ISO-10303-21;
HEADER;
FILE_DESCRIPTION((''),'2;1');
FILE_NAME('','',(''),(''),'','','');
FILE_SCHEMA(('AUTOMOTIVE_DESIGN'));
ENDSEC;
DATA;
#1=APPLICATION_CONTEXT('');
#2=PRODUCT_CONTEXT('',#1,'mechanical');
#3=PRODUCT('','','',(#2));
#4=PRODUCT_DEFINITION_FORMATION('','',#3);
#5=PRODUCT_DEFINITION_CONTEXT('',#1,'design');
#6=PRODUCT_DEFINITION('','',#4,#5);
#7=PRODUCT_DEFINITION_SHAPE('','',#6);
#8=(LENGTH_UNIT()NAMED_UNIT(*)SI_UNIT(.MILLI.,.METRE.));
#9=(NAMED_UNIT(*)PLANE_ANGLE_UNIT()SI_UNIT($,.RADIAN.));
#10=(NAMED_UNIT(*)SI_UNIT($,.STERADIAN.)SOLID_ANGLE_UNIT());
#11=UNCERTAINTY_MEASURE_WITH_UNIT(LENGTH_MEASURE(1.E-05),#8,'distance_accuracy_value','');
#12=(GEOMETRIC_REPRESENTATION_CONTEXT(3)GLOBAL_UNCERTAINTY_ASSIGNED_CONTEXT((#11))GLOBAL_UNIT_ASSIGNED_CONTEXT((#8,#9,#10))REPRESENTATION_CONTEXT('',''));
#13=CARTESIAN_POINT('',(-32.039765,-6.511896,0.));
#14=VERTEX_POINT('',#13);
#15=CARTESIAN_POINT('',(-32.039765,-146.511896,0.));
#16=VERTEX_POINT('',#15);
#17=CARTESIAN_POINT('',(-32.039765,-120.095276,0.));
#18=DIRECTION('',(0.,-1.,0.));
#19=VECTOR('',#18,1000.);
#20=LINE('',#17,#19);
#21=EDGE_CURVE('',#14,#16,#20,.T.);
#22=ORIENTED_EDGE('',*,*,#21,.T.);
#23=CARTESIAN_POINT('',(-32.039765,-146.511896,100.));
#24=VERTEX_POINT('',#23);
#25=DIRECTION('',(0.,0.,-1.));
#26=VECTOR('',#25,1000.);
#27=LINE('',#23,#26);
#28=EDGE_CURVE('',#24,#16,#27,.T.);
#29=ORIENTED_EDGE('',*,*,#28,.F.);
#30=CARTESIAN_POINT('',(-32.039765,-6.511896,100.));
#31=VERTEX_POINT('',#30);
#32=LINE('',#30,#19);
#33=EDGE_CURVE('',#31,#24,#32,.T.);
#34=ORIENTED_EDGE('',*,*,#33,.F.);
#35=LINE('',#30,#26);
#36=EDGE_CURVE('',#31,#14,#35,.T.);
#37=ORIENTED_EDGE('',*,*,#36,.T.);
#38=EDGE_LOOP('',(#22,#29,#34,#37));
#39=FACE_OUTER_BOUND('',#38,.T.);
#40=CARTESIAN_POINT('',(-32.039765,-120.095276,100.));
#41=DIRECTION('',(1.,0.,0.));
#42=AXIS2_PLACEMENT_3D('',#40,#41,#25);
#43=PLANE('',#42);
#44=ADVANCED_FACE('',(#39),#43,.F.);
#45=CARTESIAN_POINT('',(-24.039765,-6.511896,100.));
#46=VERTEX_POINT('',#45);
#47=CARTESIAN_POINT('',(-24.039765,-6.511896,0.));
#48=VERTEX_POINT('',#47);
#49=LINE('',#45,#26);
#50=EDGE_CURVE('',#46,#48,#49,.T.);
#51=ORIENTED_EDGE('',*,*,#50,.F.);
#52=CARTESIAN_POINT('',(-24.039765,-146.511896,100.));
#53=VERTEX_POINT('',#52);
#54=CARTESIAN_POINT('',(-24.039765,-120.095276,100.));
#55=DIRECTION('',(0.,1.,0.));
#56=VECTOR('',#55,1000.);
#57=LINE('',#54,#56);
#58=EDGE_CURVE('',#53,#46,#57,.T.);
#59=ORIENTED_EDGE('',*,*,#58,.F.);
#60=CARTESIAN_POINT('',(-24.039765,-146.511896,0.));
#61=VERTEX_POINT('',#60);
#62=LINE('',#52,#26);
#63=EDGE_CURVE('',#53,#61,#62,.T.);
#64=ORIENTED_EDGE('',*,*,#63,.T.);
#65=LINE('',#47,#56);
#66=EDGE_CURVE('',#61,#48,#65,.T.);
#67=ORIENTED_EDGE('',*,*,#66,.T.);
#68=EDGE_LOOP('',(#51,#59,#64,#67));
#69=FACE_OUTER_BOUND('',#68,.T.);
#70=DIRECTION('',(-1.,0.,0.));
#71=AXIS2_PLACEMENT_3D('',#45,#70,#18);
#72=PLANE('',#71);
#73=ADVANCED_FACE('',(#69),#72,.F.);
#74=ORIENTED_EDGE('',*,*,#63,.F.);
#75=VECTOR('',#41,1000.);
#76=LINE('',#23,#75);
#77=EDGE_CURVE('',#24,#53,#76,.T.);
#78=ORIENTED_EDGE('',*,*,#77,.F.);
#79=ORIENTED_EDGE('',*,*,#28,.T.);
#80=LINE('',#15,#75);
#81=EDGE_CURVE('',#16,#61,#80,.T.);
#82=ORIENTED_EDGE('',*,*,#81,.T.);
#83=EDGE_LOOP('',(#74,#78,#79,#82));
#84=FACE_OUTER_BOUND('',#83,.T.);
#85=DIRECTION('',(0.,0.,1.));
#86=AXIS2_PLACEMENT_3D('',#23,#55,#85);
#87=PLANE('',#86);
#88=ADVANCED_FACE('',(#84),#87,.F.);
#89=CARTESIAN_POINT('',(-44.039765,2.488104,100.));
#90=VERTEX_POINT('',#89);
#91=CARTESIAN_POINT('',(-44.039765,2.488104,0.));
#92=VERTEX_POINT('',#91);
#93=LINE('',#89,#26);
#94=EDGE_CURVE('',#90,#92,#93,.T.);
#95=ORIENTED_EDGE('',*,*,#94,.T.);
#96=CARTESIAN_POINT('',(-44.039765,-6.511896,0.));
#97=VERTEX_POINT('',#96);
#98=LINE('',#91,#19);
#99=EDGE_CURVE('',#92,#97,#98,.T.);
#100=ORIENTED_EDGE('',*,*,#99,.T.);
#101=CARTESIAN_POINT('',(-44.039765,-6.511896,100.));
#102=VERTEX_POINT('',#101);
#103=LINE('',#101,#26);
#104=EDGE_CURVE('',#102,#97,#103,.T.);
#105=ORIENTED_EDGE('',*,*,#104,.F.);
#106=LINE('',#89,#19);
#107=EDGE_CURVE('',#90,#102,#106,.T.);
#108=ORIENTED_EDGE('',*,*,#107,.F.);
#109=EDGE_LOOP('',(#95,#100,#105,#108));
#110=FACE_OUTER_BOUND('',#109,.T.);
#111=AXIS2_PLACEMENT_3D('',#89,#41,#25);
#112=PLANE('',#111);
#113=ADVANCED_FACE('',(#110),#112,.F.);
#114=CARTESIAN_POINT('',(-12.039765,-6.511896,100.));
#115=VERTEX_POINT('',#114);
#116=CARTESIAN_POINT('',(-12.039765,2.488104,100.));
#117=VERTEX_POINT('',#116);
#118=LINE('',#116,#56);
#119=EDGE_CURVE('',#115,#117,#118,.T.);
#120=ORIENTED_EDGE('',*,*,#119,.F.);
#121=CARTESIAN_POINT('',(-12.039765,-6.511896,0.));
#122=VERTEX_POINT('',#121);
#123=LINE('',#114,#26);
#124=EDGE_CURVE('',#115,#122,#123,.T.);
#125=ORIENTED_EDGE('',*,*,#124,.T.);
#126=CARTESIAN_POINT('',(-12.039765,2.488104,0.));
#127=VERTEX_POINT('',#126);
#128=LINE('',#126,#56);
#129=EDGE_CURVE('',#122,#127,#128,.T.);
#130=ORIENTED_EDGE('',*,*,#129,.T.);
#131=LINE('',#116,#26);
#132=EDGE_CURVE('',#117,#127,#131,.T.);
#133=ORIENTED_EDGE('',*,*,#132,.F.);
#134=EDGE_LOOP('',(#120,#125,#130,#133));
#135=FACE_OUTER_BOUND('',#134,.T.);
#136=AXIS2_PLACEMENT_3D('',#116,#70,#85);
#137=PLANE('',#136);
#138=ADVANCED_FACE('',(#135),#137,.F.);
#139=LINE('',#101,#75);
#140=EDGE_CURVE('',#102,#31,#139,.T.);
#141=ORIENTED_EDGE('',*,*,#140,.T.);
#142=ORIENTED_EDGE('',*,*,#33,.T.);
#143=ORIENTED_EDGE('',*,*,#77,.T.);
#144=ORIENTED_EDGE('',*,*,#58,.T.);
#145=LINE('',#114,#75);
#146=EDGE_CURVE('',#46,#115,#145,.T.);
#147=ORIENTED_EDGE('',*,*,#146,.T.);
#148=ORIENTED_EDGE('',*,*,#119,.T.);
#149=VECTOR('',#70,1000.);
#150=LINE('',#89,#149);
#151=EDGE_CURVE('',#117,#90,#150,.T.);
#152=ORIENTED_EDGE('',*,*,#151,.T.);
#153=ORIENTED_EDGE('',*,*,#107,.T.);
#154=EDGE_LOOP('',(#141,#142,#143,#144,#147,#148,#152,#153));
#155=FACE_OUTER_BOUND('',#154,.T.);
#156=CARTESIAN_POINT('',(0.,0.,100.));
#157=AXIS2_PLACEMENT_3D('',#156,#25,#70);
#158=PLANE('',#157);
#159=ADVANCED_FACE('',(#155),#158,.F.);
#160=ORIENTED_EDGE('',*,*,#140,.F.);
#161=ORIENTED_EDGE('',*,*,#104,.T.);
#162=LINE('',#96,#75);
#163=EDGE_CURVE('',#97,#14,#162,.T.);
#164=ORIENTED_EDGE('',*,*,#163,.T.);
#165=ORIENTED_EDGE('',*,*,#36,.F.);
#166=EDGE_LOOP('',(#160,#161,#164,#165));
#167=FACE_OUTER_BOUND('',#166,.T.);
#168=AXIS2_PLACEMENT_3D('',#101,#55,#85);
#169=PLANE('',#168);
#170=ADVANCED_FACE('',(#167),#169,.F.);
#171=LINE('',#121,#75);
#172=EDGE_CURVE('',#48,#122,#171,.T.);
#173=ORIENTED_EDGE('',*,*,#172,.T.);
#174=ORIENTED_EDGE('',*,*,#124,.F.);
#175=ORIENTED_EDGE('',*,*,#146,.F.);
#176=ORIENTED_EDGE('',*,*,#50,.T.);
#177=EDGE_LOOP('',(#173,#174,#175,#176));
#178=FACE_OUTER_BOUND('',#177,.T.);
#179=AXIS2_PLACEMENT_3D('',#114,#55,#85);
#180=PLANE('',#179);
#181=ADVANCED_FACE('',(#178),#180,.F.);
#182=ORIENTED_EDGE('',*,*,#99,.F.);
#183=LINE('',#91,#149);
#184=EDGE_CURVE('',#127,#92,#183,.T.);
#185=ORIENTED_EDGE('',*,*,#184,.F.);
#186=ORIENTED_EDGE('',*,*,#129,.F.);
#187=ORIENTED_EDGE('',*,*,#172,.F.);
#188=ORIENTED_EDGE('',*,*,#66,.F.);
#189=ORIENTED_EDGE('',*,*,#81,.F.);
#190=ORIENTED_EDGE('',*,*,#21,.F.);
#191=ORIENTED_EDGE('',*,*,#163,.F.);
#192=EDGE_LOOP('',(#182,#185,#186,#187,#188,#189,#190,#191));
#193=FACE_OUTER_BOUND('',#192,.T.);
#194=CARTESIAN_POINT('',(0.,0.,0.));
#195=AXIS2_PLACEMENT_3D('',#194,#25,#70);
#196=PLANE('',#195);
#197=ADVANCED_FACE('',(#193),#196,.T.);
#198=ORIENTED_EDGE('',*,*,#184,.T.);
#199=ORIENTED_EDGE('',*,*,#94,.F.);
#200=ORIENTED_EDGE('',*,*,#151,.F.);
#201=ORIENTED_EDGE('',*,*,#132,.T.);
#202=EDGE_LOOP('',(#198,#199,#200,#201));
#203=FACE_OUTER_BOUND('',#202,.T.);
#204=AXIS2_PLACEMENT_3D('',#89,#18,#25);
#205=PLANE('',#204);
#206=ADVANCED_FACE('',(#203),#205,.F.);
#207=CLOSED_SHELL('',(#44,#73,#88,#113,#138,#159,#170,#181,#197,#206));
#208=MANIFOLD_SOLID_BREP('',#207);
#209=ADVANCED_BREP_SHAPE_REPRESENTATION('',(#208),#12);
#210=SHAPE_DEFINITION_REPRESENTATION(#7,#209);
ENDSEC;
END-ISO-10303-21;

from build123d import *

# Parameters (mm, degrees)
EXTRUDE_1_DEPTH = 100


with BuildPart() as part:
    # 草图1 → 凸台-拉伸1 (new body)
    with BuildSketch(Plane.XY):
        Polygon((-32.039764657, -6.511895803), (-32.039764657, -120.09527648), (-32.039764657, -146.511895803), (-24.039764657, -146.511895803), (-24.039764657, -120.09527648), (-24.039764657, -6.511895803), (-12.039764657, -6.511895803), (-12.039764657, 2.488104197), (-44.039764657, 2.488104197), (-44.039764657, -6.511895803), align=None)
    extrude(amount=EXTRUDE_1_DEPTH)


solid = part.part
